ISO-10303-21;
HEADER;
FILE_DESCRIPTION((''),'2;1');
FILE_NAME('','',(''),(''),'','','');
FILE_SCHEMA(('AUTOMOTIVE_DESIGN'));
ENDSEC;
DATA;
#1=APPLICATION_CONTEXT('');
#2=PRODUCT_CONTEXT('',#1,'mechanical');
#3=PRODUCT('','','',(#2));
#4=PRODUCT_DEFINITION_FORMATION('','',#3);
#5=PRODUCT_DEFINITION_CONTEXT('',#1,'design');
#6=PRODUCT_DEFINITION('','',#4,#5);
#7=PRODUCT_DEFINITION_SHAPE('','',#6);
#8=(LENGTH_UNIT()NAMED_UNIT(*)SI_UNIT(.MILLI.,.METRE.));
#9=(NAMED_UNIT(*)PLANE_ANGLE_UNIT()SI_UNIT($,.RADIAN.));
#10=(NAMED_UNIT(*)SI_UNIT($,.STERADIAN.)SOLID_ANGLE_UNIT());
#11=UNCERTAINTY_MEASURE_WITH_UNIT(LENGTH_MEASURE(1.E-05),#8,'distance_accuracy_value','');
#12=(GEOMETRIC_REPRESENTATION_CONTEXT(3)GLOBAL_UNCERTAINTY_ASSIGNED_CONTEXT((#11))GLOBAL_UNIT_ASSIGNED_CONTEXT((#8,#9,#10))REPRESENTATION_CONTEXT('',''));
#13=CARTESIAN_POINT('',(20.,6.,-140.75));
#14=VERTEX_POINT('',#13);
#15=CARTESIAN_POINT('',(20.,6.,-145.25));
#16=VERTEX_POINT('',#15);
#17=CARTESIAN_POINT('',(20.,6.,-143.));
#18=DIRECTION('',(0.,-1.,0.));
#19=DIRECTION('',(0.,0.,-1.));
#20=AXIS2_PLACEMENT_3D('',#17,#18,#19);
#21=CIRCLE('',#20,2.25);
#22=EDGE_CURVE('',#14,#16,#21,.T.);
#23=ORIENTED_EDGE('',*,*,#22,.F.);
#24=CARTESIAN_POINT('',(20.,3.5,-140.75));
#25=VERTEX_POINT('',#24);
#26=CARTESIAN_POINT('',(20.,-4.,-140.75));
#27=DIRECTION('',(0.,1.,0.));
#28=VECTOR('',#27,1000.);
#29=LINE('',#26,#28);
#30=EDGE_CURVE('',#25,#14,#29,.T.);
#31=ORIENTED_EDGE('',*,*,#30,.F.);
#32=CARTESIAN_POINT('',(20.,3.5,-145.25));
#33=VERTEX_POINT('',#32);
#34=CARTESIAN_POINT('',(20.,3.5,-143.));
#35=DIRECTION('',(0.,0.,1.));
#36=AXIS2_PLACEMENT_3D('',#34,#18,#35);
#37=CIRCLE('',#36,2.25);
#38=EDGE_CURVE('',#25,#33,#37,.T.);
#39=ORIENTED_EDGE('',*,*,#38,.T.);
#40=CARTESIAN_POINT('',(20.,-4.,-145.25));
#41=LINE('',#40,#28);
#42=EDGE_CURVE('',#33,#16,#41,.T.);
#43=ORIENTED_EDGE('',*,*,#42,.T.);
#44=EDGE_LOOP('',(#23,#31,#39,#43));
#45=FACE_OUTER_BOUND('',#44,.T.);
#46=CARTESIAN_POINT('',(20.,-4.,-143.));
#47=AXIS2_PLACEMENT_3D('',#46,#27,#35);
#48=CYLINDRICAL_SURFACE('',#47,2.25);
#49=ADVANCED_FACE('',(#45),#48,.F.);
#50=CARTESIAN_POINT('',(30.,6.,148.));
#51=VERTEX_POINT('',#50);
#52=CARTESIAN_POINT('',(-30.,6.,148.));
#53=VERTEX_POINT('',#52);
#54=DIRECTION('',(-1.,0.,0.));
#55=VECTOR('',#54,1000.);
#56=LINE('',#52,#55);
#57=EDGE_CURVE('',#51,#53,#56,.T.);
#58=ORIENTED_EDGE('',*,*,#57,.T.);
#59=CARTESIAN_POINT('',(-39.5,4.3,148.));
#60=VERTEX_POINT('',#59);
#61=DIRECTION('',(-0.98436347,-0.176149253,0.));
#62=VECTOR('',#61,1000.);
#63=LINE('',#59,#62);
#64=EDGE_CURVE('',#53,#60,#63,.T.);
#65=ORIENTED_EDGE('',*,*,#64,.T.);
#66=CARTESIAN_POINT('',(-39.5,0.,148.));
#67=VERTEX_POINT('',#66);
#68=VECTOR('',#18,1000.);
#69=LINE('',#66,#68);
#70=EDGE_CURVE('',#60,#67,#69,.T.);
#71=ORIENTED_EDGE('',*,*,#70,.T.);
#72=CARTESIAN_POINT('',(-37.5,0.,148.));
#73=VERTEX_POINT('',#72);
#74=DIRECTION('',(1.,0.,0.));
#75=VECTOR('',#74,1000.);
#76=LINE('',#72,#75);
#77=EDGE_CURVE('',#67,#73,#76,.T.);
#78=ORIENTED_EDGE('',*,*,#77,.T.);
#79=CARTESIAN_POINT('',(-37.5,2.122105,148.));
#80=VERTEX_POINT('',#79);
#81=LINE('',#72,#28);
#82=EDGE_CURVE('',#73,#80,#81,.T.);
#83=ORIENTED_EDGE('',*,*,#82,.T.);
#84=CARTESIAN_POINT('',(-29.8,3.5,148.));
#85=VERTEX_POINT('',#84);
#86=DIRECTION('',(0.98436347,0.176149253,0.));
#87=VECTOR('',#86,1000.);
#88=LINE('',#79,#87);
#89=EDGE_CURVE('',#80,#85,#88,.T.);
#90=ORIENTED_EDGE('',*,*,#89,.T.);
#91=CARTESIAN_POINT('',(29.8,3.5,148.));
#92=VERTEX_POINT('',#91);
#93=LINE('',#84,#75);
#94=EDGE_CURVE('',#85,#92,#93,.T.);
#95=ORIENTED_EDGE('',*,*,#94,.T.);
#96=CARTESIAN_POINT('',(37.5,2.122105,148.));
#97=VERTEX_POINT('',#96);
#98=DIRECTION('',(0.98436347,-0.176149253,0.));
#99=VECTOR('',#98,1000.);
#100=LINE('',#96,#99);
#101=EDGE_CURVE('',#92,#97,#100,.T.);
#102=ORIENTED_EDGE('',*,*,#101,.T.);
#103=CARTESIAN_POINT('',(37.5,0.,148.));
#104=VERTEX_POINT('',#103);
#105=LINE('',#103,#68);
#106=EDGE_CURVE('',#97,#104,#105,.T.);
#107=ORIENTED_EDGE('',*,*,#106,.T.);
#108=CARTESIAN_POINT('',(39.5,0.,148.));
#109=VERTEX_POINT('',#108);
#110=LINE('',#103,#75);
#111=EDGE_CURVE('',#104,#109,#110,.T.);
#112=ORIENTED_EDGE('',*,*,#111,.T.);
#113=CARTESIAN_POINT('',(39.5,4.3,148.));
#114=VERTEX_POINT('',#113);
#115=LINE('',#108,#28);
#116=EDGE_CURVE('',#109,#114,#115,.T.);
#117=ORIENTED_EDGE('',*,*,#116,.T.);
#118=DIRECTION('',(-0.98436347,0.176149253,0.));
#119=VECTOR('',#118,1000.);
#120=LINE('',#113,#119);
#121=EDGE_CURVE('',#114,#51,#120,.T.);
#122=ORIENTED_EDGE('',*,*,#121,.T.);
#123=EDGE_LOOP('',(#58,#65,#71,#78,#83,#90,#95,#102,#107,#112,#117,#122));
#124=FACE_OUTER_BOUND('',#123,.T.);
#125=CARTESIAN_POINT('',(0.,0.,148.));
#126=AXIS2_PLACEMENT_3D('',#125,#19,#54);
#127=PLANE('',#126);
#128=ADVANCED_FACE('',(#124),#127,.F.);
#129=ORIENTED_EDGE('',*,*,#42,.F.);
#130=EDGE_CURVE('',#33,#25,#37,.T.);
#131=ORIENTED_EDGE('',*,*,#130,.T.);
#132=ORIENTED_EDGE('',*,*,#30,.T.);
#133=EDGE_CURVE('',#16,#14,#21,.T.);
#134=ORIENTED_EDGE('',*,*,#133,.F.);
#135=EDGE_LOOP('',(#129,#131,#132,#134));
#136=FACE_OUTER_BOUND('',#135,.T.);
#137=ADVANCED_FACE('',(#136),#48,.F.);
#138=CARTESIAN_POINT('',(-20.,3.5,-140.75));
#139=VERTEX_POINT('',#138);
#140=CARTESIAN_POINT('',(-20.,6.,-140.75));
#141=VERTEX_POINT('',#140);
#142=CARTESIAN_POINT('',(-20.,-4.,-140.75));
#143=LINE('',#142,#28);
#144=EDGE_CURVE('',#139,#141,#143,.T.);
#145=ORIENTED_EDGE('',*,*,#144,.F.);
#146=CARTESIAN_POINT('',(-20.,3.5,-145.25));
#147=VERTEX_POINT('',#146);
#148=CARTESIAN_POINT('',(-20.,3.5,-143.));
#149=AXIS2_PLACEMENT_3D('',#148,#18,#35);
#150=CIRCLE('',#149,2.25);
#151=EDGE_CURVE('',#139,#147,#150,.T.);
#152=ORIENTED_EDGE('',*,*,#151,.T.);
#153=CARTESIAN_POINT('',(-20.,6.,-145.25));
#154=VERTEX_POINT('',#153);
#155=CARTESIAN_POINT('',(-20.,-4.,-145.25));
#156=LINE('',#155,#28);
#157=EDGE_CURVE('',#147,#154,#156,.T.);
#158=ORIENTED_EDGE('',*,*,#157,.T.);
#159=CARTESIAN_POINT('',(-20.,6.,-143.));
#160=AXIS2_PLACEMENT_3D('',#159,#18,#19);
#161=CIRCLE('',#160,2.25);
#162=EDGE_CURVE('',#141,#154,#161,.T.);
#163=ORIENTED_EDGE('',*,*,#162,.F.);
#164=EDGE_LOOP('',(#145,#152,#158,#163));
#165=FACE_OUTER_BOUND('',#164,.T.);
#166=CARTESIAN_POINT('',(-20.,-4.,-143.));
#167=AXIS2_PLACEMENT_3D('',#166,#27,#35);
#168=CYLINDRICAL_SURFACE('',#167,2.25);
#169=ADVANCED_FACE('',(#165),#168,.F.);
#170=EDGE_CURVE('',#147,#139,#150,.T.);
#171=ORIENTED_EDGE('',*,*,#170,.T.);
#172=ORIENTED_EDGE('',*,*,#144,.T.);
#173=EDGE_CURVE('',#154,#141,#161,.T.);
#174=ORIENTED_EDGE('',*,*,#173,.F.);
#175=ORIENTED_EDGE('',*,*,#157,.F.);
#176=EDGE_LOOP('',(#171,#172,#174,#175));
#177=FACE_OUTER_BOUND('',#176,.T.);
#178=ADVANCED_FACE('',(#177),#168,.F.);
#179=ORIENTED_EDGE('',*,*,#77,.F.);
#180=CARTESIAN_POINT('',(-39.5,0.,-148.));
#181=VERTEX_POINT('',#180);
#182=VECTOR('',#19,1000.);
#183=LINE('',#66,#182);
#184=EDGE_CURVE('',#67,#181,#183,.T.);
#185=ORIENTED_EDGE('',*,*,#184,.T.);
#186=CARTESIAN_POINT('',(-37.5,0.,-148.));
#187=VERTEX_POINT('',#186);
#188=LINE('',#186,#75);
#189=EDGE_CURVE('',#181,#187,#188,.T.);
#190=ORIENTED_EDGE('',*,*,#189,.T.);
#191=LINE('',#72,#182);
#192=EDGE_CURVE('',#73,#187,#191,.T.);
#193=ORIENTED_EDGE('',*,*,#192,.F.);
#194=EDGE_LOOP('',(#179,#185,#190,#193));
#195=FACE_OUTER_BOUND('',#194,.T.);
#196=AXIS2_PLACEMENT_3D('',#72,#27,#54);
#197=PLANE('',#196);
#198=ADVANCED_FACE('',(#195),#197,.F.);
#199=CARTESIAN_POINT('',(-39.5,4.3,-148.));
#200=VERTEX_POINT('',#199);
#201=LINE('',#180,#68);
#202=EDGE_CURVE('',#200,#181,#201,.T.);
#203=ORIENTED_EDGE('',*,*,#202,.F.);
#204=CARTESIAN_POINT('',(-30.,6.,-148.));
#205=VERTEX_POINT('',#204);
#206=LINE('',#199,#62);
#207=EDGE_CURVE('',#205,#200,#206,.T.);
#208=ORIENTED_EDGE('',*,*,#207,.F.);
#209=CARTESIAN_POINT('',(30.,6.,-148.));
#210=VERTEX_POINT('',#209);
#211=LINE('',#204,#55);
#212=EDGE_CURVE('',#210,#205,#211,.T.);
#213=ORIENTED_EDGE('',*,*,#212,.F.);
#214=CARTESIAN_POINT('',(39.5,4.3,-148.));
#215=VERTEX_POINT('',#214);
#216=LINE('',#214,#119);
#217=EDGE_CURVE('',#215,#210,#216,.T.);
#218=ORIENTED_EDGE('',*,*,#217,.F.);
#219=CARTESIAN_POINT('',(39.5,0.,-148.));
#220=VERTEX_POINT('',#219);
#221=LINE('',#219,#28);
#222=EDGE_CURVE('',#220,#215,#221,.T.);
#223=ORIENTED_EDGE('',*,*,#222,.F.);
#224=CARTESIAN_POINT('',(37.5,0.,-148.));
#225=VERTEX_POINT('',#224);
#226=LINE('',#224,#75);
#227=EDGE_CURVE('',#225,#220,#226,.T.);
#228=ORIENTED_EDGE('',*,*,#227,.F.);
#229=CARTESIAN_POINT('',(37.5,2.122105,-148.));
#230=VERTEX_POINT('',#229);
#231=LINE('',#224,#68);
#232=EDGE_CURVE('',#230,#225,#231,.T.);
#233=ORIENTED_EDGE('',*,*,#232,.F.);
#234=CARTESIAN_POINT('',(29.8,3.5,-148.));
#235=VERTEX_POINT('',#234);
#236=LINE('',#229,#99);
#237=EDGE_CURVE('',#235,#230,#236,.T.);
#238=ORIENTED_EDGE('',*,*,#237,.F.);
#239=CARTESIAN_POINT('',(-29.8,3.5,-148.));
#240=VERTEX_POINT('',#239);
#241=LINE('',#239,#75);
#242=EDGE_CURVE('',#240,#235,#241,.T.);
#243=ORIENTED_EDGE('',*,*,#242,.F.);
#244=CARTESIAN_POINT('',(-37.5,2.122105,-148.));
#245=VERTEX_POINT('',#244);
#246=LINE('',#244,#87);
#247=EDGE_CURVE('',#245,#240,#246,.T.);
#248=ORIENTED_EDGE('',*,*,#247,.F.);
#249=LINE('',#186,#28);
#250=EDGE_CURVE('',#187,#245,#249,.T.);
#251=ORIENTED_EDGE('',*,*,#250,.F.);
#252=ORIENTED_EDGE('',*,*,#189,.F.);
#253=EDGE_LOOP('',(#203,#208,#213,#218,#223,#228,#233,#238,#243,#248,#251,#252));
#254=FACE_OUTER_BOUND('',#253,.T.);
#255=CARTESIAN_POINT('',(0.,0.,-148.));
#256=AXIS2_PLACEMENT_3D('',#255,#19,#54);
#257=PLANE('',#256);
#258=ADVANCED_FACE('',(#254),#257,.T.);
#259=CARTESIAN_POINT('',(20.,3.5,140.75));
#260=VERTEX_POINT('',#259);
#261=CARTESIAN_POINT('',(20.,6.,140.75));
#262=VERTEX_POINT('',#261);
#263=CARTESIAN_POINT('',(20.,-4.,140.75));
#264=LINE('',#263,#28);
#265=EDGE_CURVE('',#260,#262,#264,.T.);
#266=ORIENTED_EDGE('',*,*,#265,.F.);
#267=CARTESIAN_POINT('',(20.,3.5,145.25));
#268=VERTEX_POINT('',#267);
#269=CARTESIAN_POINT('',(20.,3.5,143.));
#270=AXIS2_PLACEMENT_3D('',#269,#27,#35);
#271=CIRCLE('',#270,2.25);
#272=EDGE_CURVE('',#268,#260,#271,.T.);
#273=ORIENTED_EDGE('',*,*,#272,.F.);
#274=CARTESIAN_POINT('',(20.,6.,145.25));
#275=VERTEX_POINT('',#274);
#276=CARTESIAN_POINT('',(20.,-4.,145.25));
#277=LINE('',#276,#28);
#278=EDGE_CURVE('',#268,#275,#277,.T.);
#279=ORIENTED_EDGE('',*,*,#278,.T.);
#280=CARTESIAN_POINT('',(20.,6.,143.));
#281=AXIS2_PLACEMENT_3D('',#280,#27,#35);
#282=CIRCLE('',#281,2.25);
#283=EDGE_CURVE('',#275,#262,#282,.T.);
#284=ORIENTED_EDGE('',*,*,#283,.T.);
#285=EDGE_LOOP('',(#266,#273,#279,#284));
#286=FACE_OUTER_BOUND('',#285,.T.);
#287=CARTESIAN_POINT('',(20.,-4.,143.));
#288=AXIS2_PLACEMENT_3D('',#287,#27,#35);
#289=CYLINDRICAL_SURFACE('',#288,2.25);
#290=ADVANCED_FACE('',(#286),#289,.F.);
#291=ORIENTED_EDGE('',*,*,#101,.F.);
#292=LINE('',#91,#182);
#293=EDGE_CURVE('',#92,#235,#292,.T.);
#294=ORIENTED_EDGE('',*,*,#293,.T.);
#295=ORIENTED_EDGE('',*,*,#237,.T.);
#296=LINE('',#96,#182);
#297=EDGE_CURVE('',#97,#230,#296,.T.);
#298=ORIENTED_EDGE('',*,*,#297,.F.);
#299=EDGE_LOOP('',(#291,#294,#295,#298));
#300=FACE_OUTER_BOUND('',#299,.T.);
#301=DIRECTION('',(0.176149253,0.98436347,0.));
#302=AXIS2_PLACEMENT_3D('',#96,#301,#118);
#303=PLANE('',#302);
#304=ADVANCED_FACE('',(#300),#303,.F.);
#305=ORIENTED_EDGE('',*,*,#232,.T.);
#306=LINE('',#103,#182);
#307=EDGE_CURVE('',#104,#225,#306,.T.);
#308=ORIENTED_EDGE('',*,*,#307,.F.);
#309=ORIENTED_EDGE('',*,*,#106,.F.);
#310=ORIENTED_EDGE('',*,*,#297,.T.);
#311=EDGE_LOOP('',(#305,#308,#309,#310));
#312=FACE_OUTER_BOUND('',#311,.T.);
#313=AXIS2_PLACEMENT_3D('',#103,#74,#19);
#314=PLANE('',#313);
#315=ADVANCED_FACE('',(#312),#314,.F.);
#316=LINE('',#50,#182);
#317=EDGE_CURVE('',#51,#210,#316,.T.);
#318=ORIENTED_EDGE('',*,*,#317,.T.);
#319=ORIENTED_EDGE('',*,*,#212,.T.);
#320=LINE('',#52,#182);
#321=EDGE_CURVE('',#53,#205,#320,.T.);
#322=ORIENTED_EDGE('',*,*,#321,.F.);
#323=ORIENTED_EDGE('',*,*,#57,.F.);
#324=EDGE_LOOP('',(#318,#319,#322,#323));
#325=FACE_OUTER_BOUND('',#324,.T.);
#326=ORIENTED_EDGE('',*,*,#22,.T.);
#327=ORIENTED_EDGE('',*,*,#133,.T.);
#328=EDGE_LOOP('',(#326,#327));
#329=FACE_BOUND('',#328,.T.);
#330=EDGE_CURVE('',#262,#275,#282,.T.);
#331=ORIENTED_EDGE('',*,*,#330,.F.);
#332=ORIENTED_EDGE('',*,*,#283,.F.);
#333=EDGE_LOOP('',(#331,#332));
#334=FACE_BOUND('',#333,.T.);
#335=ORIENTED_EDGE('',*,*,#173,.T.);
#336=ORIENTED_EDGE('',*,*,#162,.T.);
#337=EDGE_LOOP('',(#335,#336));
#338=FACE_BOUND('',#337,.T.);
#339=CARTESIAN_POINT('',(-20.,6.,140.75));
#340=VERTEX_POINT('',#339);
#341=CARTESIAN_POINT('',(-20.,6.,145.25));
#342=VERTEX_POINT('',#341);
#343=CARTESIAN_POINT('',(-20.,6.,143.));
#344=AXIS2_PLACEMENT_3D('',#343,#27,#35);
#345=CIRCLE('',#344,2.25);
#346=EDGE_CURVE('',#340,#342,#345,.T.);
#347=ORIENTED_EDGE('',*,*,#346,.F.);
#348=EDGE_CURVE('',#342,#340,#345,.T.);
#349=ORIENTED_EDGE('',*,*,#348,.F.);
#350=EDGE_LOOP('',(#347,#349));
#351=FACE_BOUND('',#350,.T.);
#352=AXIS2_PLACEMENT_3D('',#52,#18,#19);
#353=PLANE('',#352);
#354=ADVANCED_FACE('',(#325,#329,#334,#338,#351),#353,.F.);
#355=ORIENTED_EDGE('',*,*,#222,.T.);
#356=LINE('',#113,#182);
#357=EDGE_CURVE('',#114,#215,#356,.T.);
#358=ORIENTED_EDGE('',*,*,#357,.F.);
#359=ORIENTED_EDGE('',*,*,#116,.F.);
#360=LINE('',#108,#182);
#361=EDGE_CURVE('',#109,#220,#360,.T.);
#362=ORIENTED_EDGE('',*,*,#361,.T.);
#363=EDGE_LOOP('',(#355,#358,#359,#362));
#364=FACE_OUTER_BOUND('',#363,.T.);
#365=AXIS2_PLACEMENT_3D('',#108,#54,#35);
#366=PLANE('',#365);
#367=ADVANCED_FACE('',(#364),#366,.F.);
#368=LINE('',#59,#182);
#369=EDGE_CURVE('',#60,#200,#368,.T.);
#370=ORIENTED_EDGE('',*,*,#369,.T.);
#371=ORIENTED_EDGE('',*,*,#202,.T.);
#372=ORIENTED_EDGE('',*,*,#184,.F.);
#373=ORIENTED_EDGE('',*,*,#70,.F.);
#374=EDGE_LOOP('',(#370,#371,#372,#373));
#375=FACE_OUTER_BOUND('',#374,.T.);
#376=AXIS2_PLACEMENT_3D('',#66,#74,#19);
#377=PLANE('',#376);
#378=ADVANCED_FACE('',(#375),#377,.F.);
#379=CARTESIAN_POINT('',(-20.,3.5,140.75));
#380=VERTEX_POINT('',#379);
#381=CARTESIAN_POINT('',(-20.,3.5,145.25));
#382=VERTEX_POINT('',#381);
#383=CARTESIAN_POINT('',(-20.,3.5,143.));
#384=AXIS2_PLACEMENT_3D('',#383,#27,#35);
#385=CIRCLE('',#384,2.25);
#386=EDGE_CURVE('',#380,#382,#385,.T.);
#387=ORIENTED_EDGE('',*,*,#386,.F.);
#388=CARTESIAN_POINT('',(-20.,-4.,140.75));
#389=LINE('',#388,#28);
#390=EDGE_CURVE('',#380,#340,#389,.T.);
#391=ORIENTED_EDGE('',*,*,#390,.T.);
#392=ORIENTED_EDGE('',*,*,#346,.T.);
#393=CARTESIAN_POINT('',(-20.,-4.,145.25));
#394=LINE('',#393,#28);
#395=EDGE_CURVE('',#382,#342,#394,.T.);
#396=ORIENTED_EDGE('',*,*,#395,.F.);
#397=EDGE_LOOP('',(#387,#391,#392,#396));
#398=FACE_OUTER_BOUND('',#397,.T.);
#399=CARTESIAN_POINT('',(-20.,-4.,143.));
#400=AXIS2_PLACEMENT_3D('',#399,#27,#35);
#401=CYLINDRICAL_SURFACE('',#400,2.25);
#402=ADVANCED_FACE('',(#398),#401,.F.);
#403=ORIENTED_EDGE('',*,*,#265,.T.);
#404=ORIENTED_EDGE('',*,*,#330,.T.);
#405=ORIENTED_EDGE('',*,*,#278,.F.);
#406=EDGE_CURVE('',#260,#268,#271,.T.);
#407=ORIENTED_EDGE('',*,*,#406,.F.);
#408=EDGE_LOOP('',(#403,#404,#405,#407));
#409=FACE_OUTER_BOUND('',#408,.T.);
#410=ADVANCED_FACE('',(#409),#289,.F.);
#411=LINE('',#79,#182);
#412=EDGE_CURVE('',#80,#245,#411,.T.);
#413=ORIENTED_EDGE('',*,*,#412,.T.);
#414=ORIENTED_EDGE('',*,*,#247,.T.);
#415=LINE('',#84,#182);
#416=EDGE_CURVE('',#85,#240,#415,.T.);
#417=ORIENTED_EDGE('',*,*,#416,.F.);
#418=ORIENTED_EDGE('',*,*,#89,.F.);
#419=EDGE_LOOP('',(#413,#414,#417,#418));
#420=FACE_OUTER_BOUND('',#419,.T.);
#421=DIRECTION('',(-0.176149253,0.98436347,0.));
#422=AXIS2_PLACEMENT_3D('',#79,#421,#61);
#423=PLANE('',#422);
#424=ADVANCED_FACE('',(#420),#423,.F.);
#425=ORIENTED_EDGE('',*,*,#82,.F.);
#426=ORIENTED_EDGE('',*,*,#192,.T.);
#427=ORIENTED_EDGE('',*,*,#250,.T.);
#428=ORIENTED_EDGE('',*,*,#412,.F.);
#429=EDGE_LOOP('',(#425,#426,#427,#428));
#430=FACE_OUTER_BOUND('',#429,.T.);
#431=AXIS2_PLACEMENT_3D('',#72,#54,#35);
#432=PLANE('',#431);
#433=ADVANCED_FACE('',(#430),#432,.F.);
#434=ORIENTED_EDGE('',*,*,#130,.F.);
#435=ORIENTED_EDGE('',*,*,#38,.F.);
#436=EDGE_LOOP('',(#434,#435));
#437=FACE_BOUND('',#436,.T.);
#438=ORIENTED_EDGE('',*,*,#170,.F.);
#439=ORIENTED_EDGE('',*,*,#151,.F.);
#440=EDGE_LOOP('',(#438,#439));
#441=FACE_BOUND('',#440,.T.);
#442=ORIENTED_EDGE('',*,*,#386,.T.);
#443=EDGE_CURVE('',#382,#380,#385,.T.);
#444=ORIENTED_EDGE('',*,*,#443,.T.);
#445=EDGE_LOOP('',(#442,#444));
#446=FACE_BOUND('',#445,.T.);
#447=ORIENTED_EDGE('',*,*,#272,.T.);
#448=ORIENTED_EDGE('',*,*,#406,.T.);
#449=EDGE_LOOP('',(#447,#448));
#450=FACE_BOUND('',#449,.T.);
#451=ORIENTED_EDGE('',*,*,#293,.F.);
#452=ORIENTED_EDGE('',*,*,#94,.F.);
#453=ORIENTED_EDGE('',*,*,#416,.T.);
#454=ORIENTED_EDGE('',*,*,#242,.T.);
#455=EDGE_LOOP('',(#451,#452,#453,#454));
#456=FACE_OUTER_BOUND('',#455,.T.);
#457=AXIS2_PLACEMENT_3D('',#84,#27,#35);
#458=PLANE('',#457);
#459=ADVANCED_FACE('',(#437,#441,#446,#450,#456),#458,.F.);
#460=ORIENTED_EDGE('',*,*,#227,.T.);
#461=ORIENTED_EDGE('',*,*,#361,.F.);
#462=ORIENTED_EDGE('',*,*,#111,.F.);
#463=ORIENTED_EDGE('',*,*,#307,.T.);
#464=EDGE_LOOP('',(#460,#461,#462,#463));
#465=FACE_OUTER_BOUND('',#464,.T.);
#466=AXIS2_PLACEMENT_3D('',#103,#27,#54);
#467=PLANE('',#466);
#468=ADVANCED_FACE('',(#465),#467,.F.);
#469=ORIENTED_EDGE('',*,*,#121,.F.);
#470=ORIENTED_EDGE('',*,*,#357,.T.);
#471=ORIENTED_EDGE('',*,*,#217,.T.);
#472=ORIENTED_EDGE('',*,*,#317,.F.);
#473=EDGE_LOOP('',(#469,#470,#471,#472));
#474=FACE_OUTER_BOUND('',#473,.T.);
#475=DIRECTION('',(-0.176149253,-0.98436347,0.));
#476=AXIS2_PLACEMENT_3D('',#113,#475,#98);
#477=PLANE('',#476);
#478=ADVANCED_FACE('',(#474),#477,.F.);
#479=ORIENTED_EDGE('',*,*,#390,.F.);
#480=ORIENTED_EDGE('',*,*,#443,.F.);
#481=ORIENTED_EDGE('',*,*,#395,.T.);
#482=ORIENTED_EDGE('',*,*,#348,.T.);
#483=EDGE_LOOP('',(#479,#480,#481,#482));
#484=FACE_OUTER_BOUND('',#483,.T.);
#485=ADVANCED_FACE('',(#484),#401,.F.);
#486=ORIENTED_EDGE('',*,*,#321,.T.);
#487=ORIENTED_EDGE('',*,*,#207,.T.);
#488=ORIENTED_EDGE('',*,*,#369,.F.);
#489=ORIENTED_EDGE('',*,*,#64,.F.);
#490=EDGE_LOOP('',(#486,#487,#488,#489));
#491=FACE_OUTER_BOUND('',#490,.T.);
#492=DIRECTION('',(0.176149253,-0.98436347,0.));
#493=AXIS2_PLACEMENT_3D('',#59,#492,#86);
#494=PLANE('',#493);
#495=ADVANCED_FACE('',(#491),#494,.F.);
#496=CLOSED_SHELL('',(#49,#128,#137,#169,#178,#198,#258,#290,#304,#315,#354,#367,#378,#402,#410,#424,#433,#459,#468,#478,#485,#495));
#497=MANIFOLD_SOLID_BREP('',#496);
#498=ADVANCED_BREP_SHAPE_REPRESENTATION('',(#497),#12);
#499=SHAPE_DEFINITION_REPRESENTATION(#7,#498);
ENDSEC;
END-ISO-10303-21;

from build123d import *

# Parameters (mm, degrees)
EXTRUDE_1_DEPTH     = 148
SKETCH_2_R          = 2.25
CUT_EXTRUDE_1_DEPTH = 10


with BuildPart() as part:
    # 草图1 → 凸台-拉伸1 (new, symmetric)
    with BuildSketch(Plane.XY):
        Polygon((-37.5, 0), (-39.5, 0), (-39.5, 4.3), (-30, 6), (30, 6), (39.5, 4.3), (39.5, 0), (37.5, 0), (37.5, 2.122105263), (29.8, 3.5), (-29.8, 3.5), (-37.5, 2.122105263), align=None)
    extrude(amount=EXTRUDE_1_DEPTH, both=True)

    # 草图2 → 切除-拉伸1 (cut)
    with BuildSketch(Plane(origin=(0, 6, 0), x_dir=(1, 0, 0), z_dir=(0, 1, 0))):
        with Locations(Location((-20, -143, 0), (0, 0, 270))):
            Circle(SKETCH_2_R)
        with Locations(Location((20, -143, 0), (0, 0, 270))):
            Circle(SKETCH_2_R)
    cut_extrude_1 = extrude(amount=-CUT_EXTRUDE_1_DEPTH, mode=Mode.SUBTRACT)

    # 镜向1: 切除-拉伸1 across plane
    add(cut_extrude_1.mirror(Plane.XY), mode=Mode.SUBTRACT)


solid = part.part
